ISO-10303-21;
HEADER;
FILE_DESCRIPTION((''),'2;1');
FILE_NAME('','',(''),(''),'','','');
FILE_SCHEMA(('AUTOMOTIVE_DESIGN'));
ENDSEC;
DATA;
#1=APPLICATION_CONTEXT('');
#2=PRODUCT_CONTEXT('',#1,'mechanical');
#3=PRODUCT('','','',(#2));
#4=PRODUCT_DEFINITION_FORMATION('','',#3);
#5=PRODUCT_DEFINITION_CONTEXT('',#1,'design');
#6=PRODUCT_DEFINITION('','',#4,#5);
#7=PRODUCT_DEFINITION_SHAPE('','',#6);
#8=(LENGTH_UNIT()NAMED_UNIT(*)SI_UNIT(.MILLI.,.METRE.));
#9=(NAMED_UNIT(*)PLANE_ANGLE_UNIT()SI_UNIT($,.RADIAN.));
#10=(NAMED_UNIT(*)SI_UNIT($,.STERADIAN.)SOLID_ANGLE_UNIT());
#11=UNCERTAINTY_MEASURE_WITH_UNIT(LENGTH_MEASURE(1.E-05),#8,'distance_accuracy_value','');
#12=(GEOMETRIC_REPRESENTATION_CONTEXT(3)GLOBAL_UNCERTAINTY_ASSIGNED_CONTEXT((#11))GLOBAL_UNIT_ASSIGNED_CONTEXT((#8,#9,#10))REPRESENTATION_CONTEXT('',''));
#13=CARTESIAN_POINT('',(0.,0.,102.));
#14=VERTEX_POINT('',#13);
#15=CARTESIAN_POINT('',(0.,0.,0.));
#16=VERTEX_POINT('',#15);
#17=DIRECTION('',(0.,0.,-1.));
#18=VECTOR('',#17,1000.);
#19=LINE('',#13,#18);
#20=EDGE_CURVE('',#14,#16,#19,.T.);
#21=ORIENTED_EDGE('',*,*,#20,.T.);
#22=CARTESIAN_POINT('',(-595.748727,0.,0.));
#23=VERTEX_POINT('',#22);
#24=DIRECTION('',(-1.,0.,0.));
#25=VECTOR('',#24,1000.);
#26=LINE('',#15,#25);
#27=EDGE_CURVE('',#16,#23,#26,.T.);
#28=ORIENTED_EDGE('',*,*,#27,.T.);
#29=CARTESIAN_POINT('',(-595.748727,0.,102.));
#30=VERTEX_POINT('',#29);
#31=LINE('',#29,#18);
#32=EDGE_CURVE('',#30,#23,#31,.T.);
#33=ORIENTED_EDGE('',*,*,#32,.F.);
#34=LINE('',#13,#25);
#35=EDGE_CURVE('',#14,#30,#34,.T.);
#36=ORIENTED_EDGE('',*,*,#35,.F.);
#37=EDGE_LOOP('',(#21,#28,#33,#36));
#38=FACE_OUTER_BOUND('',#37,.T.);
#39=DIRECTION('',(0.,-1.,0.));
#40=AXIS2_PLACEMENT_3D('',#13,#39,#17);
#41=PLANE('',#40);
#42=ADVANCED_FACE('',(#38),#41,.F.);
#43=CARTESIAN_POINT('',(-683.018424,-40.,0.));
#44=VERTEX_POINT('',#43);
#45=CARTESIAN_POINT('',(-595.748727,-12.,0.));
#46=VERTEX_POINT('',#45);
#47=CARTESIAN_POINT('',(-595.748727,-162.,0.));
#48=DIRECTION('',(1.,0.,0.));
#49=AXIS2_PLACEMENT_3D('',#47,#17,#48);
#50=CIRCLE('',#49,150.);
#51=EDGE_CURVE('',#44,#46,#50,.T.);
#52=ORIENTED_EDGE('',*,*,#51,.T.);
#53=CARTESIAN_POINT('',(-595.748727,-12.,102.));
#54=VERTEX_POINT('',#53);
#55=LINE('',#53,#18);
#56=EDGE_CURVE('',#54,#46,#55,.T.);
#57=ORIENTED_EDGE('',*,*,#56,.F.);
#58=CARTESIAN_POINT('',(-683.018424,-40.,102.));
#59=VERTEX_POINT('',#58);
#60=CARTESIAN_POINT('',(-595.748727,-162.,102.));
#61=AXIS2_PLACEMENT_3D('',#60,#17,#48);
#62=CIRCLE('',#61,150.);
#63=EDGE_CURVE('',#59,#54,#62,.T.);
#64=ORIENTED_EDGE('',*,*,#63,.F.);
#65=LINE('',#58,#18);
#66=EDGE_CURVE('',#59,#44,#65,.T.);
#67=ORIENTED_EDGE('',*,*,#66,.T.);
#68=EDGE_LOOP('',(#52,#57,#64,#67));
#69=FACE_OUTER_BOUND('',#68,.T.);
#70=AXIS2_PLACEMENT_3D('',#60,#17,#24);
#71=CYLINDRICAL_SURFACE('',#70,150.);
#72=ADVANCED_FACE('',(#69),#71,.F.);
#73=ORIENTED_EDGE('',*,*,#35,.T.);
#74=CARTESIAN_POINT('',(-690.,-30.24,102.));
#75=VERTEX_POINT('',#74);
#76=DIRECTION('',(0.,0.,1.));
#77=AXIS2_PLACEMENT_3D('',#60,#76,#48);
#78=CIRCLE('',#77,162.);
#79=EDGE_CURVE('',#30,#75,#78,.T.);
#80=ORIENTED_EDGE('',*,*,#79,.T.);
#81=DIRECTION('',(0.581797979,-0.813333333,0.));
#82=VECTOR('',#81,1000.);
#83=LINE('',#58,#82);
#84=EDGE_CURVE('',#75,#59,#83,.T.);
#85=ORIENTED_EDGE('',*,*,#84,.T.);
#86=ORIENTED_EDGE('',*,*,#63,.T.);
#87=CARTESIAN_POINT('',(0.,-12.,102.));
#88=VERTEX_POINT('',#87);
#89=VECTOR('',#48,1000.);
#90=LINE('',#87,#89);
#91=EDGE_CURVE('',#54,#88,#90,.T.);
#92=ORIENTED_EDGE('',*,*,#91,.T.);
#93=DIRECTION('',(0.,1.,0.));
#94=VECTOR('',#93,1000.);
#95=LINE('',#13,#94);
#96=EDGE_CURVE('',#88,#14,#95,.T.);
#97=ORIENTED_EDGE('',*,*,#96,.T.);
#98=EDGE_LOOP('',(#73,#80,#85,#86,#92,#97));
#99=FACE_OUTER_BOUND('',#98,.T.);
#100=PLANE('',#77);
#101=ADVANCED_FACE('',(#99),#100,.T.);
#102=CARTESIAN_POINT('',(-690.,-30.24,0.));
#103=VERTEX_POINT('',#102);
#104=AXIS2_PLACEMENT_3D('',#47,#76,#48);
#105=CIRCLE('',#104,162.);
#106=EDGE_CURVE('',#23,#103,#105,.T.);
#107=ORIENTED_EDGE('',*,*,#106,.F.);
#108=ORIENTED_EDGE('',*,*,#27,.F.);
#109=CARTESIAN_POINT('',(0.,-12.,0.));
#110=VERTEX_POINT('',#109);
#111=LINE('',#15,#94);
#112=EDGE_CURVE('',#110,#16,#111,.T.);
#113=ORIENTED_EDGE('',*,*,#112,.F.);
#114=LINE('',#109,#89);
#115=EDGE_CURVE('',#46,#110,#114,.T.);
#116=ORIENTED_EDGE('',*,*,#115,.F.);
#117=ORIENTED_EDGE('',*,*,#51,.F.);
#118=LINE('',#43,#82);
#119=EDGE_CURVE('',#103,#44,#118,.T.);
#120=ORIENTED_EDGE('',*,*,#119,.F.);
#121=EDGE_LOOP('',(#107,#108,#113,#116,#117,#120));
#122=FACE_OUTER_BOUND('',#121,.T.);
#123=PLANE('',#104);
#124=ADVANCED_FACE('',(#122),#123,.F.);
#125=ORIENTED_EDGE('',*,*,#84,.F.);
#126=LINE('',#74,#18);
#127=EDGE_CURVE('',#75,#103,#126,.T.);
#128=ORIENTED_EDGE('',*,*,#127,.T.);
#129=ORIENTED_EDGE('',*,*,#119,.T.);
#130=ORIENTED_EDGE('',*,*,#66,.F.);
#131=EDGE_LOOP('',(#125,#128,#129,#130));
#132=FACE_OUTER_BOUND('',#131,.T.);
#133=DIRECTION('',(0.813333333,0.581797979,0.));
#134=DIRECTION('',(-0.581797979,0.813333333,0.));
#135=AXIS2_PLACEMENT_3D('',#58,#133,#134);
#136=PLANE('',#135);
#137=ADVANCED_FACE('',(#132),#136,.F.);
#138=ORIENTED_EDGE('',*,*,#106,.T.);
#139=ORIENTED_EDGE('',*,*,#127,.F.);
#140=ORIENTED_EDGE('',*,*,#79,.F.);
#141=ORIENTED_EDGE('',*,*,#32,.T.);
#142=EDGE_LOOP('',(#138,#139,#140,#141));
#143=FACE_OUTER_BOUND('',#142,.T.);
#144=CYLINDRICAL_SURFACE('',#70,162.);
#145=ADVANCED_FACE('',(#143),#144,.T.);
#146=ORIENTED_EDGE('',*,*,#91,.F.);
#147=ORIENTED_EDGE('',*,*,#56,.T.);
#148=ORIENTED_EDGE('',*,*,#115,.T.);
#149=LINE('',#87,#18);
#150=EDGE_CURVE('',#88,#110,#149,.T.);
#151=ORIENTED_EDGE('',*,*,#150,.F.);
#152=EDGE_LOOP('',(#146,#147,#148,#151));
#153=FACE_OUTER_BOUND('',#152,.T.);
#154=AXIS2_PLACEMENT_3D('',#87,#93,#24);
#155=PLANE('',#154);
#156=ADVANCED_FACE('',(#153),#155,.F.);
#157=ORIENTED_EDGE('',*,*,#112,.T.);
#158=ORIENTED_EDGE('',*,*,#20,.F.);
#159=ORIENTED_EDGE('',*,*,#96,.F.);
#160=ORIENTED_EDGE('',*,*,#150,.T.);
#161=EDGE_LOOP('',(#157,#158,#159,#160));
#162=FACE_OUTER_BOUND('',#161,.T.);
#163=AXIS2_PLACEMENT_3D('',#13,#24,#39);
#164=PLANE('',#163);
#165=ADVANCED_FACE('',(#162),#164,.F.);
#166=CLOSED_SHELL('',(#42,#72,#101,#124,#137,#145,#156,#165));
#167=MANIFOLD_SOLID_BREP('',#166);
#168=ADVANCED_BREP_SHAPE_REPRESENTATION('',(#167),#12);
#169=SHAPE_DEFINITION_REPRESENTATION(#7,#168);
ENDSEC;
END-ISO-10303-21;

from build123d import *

# Parameters (mm, degrees)
BOSS_EXTRUDE1_DEPTH = 102


with BuildPart() as part:
    # Sketch1 → Boss-Extrude1 (new body)
    with BuildSketch(Plane.XY):
        with BuildLine():
            Line((0, 0), (-595.74872733, 0))
            ThreePointArc((-595.74872733, 0), (-645.240544835, -7.745145943), (-690, -30.24))
            Line((-690, -30.24), (-683.018424247, -40))
            ThreePointArc((-683.018424247, -40), (-641.574484279, -19.171431429), (-595.74872733, -12))
            Line((-595.74872733, -12), (0, -12))
            Line((0, -12), (0, 0))
        make_face()
    extrude(amount=BOSS_EXTRUDE1_DEPTH)


solid = part.part
